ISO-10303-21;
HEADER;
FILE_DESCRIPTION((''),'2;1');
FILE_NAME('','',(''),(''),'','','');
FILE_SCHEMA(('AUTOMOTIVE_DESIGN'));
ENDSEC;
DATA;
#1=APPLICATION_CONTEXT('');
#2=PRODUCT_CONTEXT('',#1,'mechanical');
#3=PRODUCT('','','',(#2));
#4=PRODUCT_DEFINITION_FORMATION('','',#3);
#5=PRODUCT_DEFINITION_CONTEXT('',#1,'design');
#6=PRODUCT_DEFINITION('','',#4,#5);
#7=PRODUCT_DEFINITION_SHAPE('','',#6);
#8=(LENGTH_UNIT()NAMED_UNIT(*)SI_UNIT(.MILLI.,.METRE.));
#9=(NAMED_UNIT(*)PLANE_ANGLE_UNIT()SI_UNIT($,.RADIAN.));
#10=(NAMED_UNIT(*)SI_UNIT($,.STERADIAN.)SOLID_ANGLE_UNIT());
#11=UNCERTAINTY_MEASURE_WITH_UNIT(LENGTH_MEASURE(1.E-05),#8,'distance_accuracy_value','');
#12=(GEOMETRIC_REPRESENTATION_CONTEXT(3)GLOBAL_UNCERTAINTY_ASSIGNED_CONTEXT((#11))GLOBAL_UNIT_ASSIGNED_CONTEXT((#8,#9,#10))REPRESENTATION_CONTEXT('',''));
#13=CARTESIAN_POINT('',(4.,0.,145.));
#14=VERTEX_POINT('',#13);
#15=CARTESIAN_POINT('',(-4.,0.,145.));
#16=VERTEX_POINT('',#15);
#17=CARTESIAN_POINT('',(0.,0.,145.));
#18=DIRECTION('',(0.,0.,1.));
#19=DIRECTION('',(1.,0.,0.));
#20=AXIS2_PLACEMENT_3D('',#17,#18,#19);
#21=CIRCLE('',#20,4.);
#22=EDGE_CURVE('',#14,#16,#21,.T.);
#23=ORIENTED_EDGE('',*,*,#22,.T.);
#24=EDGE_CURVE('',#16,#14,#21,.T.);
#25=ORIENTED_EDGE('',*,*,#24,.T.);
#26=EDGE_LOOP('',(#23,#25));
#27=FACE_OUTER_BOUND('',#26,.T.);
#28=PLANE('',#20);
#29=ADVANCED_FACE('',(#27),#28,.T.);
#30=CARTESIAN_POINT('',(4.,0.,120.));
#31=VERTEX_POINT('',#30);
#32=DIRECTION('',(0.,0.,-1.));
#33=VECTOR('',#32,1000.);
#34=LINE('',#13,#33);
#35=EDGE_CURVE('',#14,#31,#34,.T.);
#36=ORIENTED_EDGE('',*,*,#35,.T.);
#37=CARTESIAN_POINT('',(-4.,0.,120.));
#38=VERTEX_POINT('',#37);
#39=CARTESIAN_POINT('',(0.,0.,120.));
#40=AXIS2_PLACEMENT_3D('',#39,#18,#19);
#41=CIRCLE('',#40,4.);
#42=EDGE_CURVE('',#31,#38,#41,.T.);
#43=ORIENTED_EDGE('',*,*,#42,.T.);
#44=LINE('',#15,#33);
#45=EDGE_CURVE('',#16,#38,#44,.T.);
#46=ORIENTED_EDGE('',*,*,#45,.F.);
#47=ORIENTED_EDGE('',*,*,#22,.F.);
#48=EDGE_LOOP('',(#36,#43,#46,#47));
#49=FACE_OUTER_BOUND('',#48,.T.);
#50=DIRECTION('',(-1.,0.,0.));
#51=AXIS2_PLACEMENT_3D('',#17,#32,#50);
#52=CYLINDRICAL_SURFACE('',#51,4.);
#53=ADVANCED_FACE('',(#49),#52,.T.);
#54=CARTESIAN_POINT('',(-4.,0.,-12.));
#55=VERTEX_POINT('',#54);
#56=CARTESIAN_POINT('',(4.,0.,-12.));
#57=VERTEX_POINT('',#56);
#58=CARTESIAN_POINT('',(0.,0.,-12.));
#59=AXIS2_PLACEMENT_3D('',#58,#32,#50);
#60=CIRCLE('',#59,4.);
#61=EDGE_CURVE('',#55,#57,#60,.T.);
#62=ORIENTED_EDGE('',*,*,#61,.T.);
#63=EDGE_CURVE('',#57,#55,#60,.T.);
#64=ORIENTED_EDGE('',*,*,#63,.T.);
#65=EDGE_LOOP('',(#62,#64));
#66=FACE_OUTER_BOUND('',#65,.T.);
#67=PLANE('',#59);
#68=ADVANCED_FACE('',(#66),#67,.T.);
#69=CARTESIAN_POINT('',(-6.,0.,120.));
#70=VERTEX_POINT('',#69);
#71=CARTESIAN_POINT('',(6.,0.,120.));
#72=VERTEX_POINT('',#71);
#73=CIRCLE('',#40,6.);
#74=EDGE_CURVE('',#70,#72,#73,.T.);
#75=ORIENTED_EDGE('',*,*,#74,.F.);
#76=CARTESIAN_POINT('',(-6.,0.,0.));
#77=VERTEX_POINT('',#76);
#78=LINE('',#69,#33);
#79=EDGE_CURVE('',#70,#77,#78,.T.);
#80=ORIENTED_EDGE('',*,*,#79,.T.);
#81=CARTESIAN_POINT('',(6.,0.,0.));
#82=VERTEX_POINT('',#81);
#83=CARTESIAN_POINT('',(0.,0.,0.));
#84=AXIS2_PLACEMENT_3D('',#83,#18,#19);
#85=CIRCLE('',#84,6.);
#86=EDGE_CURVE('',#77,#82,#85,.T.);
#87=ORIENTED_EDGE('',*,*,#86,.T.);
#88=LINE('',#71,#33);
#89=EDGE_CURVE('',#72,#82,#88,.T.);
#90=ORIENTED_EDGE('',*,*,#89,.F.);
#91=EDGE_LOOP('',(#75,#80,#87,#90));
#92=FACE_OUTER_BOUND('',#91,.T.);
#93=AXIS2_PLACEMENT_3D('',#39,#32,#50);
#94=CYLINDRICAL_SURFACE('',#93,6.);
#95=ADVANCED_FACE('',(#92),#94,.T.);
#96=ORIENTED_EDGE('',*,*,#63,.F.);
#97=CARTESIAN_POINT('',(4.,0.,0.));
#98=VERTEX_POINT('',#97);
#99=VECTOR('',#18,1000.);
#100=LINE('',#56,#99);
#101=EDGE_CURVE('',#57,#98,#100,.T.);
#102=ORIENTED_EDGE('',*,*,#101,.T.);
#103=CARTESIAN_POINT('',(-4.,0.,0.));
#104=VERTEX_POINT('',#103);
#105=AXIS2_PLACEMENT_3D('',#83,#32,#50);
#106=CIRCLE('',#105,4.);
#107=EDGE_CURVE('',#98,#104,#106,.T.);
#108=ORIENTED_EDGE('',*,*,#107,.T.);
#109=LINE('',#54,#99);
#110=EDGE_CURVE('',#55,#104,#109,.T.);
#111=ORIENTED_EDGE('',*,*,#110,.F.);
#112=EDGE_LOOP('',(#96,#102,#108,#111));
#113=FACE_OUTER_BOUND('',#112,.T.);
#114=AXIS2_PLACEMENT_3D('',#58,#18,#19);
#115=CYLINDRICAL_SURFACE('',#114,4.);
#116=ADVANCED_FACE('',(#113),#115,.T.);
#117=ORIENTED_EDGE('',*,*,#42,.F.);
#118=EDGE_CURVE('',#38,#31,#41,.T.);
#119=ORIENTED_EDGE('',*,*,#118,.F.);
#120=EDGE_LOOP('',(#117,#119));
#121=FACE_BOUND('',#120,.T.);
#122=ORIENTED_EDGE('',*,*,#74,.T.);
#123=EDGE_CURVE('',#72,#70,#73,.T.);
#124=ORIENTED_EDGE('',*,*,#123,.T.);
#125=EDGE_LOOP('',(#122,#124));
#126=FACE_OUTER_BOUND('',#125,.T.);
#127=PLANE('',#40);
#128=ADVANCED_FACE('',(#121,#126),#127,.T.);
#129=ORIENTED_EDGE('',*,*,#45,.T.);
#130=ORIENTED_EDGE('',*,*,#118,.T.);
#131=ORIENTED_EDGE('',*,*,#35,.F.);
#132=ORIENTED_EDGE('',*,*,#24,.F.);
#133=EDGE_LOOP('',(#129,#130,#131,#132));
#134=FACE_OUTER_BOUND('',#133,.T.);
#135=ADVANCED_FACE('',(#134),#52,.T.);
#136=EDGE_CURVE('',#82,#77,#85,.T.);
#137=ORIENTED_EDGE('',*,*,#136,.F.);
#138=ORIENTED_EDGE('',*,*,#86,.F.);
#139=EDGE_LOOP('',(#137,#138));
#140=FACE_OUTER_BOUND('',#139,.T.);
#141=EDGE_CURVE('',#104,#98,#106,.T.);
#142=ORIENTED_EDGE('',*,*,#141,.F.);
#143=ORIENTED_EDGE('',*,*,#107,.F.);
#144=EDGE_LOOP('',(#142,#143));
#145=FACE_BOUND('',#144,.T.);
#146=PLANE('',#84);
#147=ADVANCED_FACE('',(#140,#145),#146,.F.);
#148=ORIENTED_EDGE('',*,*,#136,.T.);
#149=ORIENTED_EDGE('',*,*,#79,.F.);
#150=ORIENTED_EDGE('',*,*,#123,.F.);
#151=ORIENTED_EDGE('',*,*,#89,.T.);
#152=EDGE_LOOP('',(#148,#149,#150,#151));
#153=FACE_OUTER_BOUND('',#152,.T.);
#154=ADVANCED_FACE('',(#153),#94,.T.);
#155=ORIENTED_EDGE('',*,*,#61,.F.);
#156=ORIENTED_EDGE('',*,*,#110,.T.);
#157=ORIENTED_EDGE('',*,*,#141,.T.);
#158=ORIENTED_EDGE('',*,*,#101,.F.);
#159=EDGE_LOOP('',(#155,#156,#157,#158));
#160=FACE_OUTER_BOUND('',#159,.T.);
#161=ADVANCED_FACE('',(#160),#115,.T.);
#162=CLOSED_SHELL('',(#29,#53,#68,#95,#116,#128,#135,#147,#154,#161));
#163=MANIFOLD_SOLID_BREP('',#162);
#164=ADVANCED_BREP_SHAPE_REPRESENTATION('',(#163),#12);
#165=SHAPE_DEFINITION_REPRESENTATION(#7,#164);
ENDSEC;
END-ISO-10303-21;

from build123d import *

# Parameters (mm, degrees)
SKETCH_1_R      = 6
EXTRUDE_1_DEPTH = 120
SKETCH_2_R      = 4
EXTRUDE_2_DEPTH = 12
EXTRUDE_START   = 25
SKETCH_3_R      = 4
EXTRUDE_3_DEPTH = 25


with BuildPart() as part:
    # 草图1 → 凸台-拉伸1 (new body)
    with BuildSketch(Plane.XY):
        Circle(SKETCH_1_R)
    extrude(amount=EXTRUDE_1_DEPTH)

    # 草图2 → 凸台-拉伸2 (add)
    with BuildSketch(Plane(origin=(0, 0, 0), x_dir=(-1, 0, 0), z_dir=(0, 0, -1))):
        Circle(SKETCH_2_R)
    extrude(amount=EXTRUDE_2_DEPTH)

    # 草图3 → 凸台-拉伸3 (add)
    with BuildSketch(Plane.XY.offset(120).offset(EXTRUDE_START)):
        with Locations(Location((0, 0, 0), (0, 0, 180))):
            Circle(SKETCH_3_R)
    extrude(amount=-EXTRUDE_3_DEPTH)


solid = part.part
